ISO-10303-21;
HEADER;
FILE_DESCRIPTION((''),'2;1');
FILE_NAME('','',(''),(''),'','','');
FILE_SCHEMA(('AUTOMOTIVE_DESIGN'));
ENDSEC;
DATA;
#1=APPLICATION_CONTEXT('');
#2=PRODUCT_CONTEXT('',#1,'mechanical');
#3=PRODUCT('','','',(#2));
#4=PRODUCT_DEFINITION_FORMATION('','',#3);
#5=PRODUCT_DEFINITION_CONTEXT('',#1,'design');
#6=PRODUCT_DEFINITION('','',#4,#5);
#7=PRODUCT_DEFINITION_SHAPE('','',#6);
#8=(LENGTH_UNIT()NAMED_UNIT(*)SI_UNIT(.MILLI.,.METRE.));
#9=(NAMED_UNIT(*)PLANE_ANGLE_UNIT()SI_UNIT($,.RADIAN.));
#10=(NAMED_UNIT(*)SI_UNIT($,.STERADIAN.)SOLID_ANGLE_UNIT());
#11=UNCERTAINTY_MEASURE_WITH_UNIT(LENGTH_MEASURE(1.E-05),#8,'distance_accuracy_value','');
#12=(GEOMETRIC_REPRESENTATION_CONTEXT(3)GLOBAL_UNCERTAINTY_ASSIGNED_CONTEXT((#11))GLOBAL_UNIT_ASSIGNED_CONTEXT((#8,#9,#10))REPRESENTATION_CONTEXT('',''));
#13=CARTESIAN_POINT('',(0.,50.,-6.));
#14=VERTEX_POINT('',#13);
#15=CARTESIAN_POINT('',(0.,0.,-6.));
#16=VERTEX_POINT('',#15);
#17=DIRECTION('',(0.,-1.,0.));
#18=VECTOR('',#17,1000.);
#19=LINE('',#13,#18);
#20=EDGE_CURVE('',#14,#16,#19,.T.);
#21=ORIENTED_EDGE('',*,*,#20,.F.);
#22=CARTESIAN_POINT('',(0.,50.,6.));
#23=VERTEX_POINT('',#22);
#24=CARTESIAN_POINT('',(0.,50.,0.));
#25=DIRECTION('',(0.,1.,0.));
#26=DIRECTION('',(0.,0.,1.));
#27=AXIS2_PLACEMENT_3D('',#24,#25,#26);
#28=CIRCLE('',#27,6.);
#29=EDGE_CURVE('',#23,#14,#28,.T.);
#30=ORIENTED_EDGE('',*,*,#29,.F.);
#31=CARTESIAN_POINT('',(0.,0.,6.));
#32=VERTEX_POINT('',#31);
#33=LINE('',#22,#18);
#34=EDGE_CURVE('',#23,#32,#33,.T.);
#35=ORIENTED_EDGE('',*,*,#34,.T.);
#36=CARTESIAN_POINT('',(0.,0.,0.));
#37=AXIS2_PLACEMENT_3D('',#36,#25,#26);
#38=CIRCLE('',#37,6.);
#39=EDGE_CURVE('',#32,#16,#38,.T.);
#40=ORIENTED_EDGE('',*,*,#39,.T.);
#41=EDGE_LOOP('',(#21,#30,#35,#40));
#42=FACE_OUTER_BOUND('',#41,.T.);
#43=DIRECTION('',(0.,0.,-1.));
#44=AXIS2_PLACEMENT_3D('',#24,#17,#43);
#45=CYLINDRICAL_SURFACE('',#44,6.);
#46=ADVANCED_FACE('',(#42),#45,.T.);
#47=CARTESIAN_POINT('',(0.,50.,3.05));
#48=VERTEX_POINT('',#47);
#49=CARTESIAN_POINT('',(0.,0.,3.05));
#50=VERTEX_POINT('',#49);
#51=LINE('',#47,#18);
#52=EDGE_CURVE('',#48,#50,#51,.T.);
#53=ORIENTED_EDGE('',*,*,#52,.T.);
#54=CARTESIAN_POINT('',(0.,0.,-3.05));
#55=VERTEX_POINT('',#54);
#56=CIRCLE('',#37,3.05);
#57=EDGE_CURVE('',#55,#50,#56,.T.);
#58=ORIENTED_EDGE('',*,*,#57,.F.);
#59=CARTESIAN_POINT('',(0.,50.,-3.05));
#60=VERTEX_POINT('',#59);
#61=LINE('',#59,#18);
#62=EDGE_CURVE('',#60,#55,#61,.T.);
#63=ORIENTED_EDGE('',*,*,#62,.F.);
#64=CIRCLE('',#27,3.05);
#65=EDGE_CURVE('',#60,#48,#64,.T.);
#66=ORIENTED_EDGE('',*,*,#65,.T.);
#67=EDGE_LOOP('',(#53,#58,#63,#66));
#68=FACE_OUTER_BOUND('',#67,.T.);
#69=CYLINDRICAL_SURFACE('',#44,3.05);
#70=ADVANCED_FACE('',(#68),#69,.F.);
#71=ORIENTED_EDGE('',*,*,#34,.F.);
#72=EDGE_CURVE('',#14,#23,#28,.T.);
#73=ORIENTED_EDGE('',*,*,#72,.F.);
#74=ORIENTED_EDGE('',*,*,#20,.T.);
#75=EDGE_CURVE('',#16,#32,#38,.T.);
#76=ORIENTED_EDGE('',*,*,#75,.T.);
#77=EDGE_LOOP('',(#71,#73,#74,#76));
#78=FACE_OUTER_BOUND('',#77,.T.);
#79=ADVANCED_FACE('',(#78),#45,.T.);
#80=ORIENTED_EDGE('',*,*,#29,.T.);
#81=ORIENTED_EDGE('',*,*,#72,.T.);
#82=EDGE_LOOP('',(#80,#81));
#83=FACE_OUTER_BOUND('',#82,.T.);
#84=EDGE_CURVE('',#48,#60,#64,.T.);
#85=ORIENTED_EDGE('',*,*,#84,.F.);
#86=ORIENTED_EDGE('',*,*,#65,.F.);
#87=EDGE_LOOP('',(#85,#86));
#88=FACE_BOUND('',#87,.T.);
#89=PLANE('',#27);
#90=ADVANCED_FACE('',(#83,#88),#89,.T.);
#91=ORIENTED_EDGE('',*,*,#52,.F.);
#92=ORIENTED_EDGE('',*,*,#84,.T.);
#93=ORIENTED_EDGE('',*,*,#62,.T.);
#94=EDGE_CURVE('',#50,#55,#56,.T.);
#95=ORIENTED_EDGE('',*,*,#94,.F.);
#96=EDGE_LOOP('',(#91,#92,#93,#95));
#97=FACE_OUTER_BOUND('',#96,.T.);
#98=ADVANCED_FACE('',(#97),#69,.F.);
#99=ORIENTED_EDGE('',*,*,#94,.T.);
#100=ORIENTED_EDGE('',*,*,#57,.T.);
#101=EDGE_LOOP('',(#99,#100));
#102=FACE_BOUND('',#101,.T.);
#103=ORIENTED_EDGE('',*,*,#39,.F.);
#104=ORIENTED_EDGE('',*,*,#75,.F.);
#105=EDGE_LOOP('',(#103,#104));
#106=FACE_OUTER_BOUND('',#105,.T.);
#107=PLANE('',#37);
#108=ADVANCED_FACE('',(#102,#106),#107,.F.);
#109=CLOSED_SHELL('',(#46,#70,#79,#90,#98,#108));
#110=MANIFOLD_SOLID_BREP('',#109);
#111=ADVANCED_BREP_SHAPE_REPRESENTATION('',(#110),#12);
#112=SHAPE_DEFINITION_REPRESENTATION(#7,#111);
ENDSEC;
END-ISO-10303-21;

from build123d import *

# Parameters (mm, degrees)
SKETCH1_R           = 6
SKETCH1_R_2         = 3.05
BOSS_EXTRUDE1_DEPTH = 50


with BuildPart() as part:
    # Sketch1 → Boss-Extrude1 (new body)
    with BuildSketch(Plane(origin=(0, 0, 0), x_dir=(1, 0, 0), z_dir=(0, 1, 0))):
        with Locations(Location((0, 0, 0), (0, 0, 270))):
            Circle(SKETCH1_R)
        with Locations(Location((0, 0, 0), (0, 0, 270))):
            Circle(SKETCH1_R_2, mode=Mode.SUBTRACT)
    extrude(amount=BOSS_EXTRUDE1_DEPTH)


solid = part.part
